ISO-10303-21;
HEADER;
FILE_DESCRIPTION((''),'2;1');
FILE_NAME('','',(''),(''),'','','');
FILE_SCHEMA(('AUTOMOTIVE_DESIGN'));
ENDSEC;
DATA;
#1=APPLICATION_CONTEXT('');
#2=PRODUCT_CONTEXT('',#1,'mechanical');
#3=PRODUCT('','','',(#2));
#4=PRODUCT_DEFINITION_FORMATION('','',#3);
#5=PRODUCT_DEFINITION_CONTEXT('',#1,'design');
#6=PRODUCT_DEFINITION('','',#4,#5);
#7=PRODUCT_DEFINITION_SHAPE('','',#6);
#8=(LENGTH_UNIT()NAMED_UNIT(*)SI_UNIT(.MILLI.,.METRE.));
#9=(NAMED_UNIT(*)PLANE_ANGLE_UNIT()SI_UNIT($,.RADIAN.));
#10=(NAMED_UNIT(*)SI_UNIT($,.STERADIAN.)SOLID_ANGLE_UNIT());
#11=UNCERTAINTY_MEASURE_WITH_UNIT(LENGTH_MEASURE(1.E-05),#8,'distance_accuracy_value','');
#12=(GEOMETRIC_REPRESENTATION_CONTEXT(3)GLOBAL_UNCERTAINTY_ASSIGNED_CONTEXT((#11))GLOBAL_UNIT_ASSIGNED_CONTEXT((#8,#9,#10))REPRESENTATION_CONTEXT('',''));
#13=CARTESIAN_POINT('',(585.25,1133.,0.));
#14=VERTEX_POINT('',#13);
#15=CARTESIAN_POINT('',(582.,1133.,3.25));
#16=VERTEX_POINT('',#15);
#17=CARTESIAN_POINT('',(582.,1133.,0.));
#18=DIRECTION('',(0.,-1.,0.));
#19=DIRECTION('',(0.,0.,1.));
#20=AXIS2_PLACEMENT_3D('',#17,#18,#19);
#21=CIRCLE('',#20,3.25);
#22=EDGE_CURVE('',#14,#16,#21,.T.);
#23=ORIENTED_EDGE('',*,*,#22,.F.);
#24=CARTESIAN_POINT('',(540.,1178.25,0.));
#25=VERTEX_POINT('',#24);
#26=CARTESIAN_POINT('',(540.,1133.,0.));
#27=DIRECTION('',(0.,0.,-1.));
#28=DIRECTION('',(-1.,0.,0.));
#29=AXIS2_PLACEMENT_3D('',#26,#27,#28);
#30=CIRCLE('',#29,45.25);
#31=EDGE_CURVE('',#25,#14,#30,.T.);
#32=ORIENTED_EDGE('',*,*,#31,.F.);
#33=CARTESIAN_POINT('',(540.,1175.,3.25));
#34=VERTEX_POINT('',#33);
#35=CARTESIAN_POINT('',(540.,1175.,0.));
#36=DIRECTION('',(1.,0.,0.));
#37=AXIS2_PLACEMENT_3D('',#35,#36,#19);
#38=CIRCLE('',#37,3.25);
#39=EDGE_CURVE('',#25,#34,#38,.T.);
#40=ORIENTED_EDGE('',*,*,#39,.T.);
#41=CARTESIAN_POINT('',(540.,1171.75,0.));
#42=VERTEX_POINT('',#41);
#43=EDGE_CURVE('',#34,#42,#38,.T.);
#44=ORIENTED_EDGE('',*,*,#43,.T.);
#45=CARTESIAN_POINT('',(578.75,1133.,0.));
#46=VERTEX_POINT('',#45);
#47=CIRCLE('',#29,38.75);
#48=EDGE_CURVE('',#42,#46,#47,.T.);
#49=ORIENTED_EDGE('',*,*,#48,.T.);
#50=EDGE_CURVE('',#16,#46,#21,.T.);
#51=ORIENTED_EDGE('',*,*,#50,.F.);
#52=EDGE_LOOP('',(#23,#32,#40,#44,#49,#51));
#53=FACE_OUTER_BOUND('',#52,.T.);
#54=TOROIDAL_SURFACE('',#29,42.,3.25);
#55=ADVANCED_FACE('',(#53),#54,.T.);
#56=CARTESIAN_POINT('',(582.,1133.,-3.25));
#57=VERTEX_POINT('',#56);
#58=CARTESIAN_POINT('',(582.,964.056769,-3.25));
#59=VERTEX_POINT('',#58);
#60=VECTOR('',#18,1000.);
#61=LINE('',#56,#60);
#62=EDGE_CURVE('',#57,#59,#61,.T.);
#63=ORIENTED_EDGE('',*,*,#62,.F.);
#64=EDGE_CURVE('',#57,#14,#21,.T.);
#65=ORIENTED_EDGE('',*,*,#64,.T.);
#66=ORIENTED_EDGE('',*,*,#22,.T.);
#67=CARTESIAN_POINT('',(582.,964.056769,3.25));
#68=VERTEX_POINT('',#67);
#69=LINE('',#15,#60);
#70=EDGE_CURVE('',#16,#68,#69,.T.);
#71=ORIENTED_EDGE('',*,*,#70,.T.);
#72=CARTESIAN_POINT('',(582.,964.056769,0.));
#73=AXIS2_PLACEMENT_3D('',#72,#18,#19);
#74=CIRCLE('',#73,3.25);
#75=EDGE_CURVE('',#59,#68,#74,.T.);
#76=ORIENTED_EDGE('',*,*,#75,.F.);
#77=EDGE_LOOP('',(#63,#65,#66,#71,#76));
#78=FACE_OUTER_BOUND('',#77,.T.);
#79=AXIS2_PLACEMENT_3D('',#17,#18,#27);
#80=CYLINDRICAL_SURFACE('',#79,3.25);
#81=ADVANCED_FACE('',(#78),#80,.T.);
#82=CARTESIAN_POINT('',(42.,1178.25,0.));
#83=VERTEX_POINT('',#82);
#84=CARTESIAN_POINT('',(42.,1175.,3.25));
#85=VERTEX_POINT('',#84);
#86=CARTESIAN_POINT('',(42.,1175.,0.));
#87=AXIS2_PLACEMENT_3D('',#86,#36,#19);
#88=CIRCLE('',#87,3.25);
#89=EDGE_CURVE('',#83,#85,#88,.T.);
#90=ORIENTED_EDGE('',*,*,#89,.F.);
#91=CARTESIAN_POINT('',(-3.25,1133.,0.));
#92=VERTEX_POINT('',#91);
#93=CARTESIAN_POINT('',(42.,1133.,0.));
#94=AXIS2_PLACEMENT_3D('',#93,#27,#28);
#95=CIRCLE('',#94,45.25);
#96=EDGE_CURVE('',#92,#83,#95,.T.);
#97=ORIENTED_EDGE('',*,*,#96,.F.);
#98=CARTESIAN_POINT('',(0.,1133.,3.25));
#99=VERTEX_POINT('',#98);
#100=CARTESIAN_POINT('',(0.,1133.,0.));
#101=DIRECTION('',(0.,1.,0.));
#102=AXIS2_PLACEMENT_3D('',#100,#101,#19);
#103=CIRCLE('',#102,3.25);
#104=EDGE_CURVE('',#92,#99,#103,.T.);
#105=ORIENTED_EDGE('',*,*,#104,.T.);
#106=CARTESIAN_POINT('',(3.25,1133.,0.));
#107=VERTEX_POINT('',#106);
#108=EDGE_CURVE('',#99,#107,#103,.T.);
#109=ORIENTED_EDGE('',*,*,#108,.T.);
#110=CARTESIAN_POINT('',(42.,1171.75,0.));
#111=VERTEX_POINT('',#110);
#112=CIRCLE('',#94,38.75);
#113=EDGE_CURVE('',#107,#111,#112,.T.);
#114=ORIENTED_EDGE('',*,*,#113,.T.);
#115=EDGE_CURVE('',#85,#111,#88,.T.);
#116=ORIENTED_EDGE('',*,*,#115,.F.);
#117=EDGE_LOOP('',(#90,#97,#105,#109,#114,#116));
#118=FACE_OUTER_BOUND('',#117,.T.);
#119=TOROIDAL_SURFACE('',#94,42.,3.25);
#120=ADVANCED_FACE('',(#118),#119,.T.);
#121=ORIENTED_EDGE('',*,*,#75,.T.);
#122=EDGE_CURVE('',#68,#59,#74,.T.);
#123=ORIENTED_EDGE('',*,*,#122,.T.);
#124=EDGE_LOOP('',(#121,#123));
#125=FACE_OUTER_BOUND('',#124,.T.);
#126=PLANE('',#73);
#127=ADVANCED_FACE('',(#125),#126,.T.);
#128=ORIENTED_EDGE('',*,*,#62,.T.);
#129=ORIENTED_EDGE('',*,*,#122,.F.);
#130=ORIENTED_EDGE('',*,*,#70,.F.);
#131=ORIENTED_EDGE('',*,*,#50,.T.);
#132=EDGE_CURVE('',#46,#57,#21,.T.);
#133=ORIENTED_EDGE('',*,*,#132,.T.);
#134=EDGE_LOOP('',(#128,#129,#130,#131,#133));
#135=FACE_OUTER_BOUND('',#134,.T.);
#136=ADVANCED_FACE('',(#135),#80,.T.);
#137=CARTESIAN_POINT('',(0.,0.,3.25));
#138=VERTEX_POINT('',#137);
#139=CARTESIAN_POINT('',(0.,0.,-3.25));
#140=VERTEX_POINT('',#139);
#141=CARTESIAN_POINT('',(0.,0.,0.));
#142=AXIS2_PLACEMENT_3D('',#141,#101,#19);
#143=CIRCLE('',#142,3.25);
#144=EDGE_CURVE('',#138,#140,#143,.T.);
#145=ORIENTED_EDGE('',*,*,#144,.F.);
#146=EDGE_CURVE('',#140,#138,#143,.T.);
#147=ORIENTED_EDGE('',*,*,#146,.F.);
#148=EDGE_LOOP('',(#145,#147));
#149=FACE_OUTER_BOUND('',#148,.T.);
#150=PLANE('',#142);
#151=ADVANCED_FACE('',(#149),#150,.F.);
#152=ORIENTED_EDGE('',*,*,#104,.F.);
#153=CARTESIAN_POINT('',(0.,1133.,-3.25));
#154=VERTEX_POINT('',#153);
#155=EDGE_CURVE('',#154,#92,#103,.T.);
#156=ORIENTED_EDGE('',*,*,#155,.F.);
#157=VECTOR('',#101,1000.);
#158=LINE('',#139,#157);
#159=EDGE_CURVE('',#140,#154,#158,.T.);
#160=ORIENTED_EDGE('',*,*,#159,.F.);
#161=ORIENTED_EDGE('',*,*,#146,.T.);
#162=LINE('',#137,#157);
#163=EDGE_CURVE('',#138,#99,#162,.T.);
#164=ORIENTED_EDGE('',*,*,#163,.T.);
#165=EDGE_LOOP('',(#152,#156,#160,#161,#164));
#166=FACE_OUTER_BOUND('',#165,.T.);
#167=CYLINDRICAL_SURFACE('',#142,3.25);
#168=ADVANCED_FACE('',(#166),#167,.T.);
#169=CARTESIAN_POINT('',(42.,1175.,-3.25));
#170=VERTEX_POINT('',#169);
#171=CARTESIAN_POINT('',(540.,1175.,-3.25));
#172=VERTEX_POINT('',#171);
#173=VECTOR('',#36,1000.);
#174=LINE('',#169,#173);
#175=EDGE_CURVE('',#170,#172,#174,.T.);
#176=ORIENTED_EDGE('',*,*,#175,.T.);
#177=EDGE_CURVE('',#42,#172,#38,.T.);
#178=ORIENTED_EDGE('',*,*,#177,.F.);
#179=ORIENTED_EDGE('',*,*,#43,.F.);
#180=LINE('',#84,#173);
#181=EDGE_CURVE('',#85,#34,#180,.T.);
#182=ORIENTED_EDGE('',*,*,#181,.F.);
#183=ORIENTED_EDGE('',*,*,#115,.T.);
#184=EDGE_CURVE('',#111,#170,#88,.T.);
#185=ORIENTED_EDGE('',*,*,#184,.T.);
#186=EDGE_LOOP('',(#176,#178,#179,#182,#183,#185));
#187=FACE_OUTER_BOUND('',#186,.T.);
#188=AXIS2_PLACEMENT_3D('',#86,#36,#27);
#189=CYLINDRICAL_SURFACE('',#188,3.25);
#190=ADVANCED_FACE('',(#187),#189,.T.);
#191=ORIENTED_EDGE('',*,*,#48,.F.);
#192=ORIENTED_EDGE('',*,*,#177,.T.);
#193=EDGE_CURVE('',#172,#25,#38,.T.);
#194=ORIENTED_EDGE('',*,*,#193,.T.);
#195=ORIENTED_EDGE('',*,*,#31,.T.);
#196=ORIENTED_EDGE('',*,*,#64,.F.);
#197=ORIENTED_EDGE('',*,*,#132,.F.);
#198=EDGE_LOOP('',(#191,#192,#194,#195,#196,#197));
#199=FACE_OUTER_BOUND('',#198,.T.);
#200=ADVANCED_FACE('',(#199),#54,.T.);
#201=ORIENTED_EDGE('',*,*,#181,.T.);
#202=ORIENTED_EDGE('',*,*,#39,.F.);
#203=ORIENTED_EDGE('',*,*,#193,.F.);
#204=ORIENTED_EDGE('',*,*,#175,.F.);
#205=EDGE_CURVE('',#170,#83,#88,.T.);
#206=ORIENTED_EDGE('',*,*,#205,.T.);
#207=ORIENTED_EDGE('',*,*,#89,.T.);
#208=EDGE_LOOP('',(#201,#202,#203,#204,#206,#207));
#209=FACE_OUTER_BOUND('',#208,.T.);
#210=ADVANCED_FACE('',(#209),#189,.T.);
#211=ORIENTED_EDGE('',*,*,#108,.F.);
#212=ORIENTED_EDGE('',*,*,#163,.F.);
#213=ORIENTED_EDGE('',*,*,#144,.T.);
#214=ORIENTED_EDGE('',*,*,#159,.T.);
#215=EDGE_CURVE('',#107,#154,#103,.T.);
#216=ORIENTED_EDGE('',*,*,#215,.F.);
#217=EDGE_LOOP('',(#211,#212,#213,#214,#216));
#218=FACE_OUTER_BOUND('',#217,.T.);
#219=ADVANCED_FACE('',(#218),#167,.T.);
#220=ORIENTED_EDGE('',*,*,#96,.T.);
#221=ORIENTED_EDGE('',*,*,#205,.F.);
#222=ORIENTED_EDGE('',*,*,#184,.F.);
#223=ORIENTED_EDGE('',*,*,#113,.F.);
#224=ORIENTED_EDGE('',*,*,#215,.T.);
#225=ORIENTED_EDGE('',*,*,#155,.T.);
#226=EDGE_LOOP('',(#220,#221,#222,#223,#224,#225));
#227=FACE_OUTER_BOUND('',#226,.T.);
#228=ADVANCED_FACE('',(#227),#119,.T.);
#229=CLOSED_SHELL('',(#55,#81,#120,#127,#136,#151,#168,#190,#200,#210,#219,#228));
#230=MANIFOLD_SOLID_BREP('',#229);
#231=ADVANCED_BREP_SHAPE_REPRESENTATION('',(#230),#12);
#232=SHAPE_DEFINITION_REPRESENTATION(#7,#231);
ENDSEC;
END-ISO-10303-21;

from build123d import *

# Parameters (mm, degrees)
SKETCH2_R = 3.25


with BuildPart() as part:
    # Sweep1: sweep along a path in Sketch1
    with BuildLine(Plane.XY) as sweep1_path:
        Line((0, 0), (0, 1133))
        ThreePointArc((0, 1133), (12.30151519, 1162.69848481), (42, 1175))
        Line((42, 1175), (540, 1175))
        ThreePointArc((540, 1175), (569.69848481, 1162.69848481), (582, 1133))
        Line((582, 1133), (582, 964.056768559))
    # Sketch2 → Sweep1 (sweep)
    with BuildSketch(Plane(origin=(0, 0, 0), x_dir=(1, 0, 0), z_dir=(0, 1, 0))):
        Circle(SKETCH2_R)
    sweep(path=sweep1_path.line)


solid = part.part
